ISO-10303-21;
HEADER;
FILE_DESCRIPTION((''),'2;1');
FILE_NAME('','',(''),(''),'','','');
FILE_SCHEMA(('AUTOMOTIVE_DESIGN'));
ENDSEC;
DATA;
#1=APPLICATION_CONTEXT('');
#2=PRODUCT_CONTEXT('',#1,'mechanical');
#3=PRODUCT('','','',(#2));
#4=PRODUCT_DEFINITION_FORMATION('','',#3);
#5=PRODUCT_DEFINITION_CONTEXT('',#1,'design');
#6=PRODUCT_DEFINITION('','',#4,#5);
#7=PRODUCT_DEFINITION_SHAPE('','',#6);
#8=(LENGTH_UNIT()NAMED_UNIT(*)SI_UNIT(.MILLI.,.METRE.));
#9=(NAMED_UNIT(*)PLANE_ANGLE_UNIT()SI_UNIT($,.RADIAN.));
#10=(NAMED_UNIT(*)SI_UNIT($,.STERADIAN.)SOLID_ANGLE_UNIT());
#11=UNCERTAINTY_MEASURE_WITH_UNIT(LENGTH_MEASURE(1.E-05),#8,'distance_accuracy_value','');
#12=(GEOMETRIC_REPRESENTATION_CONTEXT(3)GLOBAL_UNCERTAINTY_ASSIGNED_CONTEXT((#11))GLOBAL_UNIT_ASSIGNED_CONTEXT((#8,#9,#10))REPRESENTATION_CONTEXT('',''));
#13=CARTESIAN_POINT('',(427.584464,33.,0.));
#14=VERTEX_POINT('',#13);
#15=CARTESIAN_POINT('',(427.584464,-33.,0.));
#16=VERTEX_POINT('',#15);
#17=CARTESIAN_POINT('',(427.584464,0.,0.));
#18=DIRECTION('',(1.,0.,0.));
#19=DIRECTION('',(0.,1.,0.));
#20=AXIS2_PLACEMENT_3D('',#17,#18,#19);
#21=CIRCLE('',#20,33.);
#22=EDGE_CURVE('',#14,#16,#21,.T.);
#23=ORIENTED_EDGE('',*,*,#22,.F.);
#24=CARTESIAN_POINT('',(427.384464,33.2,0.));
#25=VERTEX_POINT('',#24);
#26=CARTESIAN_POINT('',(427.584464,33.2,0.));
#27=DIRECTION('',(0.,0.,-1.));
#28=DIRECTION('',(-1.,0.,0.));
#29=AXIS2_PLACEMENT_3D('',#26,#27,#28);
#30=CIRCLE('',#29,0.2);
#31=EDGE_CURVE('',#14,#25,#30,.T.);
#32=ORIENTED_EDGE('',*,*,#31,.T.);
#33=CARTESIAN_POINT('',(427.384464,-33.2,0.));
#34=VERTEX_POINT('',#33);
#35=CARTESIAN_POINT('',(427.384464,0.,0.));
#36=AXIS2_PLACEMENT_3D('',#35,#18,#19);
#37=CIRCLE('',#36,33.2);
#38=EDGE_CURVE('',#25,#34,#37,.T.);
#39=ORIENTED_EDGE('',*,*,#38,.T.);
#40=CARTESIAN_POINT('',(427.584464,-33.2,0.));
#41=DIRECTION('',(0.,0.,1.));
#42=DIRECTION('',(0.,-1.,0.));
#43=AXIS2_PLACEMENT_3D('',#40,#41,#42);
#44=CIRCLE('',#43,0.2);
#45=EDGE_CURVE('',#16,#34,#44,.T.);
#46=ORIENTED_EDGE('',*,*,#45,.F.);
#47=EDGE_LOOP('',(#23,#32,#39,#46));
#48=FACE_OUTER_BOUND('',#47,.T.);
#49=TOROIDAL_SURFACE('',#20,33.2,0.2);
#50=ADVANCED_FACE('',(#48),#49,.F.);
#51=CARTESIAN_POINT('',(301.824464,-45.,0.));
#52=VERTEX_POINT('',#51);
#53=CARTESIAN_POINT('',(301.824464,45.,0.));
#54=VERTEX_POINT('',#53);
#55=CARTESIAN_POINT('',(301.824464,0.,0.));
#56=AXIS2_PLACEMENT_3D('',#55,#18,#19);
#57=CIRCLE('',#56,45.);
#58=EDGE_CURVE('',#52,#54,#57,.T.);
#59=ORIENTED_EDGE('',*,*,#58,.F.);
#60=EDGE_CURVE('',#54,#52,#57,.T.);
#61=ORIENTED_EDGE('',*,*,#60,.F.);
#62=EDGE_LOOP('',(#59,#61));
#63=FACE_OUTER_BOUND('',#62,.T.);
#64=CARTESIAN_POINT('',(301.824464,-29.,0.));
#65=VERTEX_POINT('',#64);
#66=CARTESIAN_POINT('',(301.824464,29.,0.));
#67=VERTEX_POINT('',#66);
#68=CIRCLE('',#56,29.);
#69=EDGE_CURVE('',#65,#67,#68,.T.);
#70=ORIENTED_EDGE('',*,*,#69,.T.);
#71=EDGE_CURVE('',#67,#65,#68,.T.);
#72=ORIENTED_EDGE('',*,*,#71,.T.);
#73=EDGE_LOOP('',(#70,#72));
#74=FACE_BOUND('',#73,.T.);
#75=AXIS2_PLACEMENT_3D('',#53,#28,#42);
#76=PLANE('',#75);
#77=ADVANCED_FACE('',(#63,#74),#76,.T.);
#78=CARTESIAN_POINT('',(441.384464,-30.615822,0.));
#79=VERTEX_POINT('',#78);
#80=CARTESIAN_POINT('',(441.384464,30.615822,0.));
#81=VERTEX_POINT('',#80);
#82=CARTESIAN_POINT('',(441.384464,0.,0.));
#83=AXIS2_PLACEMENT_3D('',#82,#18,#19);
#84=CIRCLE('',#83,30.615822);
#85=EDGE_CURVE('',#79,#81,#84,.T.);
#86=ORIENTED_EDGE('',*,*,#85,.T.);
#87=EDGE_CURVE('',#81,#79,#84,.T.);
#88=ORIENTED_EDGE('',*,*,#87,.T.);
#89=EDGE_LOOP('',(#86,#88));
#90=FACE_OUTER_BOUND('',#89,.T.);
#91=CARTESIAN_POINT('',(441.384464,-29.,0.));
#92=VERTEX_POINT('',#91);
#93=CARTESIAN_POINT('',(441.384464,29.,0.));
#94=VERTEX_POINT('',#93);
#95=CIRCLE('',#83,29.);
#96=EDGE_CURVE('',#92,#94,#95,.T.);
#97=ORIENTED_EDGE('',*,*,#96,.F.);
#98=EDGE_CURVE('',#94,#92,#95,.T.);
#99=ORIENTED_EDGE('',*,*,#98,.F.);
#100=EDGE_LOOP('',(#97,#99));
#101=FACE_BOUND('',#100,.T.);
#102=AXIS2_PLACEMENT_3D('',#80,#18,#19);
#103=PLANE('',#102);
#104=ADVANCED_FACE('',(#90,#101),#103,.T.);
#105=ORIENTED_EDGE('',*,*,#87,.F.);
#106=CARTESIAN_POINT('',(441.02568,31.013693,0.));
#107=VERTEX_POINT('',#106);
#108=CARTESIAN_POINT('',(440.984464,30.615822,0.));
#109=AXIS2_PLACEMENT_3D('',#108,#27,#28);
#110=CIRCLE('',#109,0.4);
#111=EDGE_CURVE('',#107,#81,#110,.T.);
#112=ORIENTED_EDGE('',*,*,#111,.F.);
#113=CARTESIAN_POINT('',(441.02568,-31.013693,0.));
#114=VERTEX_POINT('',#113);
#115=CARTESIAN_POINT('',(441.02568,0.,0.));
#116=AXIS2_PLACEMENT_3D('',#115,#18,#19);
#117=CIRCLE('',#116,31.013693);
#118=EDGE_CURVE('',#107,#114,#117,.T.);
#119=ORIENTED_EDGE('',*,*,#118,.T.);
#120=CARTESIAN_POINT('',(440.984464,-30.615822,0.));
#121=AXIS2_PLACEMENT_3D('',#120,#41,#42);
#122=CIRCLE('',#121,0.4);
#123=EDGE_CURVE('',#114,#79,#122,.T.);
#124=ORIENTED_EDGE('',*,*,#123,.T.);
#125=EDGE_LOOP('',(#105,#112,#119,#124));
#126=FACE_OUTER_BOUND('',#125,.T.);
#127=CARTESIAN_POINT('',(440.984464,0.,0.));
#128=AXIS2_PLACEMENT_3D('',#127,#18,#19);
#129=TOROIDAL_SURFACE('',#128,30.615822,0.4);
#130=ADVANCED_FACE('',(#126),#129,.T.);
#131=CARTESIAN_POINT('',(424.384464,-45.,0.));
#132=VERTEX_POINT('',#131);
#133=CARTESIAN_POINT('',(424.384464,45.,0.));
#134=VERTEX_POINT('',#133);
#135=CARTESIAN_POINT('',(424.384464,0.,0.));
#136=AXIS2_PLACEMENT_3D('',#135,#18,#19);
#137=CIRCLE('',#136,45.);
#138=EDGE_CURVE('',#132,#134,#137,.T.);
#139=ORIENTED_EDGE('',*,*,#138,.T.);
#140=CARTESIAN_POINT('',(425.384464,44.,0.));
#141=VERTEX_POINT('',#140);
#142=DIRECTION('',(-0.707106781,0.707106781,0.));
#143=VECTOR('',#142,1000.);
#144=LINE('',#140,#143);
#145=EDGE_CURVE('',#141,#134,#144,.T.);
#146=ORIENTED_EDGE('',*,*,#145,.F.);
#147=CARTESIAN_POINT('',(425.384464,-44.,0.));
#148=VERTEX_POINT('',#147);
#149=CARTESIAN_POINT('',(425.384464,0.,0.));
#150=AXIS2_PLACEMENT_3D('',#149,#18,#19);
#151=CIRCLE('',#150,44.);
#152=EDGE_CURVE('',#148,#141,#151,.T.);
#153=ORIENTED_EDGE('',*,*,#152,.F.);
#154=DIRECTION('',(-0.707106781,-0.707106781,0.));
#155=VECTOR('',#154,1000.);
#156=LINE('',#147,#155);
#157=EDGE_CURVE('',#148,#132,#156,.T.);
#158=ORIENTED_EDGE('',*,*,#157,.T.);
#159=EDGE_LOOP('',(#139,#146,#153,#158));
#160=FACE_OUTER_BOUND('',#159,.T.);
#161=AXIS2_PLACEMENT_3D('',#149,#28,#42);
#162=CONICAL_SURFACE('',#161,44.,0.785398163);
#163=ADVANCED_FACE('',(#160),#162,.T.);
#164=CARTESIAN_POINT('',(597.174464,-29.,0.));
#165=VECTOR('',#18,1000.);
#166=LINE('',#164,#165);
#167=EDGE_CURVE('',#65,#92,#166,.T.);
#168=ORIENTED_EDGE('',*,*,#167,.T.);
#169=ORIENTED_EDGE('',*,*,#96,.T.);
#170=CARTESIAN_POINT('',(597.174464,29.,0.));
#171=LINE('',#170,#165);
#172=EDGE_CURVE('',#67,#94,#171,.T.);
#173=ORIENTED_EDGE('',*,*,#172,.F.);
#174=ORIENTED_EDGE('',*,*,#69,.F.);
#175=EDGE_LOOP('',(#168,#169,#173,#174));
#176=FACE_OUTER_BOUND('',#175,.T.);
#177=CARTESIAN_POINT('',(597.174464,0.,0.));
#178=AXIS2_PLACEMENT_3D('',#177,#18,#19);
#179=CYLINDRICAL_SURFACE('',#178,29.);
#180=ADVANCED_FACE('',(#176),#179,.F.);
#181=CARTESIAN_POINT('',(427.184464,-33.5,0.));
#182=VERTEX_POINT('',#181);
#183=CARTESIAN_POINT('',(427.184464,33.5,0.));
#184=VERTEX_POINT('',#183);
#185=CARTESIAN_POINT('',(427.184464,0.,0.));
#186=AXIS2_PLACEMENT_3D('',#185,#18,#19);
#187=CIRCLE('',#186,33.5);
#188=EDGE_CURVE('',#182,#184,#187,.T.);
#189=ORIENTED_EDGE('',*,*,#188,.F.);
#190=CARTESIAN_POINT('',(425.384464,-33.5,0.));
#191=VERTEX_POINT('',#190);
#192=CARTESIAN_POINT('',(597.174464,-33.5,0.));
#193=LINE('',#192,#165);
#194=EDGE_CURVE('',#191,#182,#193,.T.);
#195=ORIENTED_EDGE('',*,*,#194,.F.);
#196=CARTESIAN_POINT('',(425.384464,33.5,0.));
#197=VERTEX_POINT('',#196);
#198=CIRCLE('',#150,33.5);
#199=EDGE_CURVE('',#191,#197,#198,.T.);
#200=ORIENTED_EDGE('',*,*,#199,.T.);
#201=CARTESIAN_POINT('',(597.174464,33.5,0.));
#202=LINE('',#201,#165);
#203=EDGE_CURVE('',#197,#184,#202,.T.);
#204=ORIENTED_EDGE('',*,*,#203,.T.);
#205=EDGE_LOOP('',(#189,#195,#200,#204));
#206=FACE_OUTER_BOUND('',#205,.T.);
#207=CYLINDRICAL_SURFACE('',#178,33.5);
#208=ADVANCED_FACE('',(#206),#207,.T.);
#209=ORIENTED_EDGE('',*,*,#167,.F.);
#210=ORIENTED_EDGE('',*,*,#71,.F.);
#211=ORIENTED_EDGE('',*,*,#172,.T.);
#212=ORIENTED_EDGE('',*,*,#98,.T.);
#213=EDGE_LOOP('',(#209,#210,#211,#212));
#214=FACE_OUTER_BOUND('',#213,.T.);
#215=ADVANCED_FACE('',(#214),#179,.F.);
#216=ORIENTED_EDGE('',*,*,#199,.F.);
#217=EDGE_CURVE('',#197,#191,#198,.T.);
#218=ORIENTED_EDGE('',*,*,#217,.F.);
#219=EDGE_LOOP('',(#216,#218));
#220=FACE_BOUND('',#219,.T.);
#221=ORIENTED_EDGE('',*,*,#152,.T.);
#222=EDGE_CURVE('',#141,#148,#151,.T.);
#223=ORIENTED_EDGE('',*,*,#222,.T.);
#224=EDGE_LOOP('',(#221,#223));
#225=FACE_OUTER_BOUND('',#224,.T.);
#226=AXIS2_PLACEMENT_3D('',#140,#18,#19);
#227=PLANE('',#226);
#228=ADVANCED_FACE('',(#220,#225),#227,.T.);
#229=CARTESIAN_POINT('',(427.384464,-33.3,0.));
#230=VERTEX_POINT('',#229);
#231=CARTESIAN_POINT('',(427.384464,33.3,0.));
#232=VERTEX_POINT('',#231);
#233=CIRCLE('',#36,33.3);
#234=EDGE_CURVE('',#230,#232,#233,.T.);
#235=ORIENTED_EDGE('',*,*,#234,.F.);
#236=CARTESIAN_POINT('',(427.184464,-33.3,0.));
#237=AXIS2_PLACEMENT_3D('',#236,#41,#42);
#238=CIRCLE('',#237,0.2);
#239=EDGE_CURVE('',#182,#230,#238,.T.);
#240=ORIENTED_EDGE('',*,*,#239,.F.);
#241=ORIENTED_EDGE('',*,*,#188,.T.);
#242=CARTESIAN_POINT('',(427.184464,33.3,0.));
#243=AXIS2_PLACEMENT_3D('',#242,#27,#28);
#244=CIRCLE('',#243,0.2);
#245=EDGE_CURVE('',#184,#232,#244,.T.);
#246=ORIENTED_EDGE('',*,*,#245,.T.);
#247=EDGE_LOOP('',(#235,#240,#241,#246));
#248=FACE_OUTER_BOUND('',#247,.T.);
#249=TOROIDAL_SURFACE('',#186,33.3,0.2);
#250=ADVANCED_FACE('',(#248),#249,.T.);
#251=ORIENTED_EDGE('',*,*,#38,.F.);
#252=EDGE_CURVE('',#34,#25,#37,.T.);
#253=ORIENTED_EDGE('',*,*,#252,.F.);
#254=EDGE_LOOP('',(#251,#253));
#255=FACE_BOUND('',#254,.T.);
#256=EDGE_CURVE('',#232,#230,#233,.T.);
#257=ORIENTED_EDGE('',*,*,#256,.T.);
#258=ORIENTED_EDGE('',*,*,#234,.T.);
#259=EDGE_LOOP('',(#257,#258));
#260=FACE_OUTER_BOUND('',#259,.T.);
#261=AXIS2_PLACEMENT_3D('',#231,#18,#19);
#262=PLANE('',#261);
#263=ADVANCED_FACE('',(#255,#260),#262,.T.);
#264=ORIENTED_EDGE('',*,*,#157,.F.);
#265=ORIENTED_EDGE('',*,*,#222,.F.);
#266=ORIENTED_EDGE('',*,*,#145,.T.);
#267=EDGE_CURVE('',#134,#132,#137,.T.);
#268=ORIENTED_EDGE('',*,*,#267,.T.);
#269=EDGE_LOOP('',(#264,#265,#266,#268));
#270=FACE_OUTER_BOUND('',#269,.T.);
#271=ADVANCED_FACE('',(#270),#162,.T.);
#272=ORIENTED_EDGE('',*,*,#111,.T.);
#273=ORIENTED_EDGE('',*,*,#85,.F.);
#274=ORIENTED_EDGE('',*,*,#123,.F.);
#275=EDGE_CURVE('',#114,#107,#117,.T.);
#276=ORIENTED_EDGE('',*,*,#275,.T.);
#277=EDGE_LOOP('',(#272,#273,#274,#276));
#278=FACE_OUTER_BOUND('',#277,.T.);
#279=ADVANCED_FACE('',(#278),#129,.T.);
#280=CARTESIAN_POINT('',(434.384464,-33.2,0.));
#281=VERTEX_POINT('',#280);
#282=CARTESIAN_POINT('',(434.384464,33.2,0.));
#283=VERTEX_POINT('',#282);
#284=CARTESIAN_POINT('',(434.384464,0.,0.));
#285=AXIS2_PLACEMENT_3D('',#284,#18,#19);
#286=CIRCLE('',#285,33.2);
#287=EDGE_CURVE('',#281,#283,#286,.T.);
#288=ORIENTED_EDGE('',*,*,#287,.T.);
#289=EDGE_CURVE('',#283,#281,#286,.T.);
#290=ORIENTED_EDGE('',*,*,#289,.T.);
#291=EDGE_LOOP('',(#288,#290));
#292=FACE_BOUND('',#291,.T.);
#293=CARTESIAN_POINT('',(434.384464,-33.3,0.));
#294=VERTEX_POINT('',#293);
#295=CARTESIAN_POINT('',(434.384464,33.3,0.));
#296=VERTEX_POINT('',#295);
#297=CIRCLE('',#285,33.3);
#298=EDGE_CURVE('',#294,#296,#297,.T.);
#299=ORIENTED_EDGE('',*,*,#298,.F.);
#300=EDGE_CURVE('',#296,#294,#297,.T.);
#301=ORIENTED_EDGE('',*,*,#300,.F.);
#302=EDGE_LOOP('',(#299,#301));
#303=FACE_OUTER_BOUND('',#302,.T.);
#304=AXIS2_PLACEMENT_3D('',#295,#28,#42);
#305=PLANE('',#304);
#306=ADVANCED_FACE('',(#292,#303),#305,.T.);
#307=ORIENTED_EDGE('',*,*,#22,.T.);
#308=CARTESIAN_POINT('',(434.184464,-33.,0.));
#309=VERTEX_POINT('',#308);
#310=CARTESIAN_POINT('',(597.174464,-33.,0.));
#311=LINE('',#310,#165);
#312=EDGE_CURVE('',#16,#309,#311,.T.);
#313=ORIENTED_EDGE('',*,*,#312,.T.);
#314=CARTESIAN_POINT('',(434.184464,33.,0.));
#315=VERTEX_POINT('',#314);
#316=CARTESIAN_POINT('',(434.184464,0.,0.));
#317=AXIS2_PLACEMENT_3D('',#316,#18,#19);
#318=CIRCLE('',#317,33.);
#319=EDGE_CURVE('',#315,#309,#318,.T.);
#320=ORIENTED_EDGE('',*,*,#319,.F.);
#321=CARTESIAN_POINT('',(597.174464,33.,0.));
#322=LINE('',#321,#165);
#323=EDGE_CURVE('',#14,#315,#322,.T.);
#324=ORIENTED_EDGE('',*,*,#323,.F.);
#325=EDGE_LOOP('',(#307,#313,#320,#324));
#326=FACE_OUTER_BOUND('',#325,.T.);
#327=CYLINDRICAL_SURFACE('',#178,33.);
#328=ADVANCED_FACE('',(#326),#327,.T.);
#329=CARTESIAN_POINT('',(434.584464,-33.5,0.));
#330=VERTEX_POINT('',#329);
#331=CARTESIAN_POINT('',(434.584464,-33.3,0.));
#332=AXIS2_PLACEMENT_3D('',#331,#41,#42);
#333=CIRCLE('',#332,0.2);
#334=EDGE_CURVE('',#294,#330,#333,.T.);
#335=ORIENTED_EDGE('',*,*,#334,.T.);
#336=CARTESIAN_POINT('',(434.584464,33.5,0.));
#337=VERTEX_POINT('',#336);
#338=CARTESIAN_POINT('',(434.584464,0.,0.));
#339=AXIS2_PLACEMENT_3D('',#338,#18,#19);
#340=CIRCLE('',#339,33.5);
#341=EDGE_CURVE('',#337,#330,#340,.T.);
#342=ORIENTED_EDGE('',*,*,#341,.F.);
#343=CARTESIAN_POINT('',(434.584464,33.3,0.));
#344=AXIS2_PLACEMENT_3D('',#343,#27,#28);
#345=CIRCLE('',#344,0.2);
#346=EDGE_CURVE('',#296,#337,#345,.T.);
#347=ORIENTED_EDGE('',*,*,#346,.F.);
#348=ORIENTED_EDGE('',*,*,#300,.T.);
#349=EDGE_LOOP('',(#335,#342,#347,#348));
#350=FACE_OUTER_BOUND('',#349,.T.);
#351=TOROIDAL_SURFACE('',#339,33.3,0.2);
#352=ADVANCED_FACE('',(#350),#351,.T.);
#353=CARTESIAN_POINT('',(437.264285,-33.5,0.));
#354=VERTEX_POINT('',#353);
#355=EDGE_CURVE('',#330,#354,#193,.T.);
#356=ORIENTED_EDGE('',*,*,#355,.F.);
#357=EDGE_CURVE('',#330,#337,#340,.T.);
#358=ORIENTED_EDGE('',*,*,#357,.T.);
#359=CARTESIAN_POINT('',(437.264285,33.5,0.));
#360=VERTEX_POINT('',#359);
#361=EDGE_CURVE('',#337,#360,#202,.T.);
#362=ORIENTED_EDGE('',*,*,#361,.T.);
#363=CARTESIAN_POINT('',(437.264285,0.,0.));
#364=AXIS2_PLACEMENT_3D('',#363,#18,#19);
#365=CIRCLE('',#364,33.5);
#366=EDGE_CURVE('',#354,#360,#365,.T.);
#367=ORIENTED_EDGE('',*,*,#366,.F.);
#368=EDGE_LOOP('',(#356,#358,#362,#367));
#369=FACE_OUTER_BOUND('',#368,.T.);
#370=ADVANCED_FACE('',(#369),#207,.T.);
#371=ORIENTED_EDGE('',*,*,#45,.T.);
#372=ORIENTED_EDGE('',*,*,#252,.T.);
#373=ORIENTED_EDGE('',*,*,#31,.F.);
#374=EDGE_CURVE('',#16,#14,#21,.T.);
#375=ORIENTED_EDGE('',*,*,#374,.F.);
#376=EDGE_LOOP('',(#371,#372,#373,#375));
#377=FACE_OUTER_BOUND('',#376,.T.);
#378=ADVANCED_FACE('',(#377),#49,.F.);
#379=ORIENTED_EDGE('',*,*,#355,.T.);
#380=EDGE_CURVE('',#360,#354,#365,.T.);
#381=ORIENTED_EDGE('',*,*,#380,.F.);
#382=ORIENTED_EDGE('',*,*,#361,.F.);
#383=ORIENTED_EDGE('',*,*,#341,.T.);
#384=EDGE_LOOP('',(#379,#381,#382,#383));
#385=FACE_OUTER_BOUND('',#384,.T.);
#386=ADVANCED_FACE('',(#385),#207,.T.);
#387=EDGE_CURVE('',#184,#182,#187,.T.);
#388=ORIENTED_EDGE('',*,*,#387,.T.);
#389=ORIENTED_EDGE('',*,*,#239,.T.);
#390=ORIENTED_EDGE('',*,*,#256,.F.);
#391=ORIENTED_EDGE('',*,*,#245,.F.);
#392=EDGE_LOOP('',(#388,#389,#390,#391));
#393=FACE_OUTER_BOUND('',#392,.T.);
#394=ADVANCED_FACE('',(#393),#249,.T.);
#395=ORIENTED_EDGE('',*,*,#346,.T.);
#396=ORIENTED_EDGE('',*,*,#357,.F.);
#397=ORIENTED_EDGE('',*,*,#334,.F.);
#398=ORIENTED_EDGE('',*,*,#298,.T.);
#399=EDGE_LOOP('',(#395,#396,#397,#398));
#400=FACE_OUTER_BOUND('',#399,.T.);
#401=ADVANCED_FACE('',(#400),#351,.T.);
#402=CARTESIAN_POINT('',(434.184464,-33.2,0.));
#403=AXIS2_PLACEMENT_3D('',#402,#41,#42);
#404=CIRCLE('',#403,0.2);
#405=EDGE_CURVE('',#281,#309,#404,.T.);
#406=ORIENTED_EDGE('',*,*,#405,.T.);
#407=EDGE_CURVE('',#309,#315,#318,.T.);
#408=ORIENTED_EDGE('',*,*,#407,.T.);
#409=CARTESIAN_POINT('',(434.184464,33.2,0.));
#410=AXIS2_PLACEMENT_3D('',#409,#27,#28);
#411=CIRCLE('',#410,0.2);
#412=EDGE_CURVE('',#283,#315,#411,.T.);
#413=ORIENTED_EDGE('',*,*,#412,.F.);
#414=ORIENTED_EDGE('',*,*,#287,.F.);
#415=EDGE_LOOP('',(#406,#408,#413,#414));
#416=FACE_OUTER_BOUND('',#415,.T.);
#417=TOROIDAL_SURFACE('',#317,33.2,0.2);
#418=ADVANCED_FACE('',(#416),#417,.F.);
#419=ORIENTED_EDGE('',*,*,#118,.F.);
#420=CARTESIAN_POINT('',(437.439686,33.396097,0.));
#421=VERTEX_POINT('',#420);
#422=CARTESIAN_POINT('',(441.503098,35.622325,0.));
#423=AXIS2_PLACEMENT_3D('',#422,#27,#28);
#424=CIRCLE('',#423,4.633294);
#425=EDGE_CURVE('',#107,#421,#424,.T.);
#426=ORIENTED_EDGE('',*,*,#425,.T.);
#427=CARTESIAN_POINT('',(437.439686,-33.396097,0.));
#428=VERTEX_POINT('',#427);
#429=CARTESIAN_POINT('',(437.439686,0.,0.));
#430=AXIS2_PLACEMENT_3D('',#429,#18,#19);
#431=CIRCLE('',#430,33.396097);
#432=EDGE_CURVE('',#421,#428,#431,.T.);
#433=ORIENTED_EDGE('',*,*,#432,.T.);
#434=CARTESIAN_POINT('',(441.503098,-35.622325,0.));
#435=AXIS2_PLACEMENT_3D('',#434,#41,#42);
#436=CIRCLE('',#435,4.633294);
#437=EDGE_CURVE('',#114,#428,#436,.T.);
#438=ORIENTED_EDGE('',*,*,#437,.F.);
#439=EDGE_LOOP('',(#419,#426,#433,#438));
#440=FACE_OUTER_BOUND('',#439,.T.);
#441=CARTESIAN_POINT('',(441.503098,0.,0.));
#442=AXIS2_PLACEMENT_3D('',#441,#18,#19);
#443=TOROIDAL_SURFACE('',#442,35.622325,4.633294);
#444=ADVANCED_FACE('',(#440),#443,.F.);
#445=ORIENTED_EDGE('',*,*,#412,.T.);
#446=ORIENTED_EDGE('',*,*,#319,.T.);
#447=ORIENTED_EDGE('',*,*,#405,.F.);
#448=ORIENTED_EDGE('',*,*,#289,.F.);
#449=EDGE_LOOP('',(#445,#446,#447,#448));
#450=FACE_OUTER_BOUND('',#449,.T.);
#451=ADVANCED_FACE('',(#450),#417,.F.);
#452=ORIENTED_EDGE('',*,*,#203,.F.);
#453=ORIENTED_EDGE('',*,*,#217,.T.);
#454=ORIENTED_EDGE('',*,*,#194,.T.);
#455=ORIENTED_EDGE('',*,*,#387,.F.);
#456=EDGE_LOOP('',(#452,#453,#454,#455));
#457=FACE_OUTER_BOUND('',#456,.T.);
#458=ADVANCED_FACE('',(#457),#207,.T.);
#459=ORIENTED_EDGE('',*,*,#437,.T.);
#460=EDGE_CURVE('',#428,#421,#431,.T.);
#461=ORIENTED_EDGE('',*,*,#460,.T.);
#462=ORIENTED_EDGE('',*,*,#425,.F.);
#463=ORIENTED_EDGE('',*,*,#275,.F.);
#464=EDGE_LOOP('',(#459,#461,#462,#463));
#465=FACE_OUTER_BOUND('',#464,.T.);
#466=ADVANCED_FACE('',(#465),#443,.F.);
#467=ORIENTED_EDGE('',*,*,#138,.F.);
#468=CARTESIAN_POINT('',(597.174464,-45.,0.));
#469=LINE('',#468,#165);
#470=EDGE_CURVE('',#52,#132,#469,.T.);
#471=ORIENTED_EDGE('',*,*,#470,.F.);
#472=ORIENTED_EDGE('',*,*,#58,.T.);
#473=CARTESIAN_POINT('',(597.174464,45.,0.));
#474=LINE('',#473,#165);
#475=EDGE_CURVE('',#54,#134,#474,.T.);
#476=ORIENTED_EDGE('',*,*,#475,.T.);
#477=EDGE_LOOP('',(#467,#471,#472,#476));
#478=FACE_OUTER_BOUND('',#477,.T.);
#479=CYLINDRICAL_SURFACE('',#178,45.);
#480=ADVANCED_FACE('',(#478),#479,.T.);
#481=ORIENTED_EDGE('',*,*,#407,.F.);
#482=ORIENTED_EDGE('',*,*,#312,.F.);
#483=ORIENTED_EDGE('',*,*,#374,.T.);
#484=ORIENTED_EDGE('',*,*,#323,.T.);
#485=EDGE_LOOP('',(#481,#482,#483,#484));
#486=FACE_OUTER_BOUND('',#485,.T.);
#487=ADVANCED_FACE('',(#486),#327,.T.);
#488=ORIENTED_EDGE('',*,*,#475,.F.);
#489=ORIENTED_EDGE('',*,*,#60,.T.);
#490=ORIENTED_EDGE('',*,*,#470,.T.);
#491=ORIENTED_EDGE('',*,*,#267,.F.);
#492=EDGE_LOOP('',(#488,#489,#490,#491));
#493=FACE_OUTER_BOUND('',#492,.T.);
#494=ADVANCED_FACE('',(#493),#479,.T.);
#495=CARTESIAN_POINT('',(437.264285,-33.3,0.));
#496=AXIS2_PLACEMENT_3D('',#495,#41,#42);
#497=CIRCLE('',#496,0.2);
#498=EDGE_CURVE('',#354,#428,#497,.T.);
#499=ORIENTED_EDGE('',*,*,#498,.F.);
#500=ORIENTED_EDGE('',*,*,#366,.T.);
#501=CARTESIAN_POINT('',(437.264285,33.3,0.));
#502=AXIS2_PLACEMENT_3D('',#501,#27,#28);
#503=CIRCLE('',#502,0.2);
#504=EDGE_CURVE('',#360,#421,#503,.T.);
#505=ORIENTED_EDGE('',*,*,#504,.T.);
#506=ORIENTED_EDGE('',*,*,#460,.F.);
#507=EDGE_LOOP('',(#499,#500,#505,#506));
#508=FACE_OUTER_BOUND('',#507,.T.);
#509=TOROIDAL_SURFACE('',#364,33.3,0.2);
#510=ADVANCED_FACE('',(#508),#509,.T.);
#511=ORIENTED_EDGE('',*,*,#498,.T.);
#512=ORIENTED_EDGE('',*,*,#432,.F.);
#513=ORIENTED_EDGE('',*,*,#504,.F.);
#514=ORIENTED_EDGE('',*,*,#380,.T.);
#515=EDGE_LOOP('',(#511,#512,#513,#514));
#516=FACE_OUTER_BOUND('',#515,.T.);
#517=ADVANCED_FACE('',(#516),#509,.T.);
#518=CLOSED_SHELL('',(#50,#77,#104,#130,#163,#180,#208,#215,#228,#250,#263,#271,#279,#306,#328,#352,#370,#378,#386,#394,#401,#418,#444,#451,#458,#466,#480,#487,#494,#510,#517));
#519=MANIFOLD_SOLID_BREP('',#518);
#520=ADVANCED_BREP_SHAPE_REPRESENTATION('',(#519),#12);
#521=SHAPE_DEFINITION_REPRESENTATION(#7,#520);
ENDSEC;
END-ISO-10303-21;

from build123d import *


with BuildPart() as part:
    # Sketch1 → Revolve1 (revolve)
    with BuildSketch(Plane.XY):
        with BuildLine():
            Line((437.264284999, 33.5), (434.584463757, 33.5))
            ThreePointArc((434.584463757, 33.5), (434.443042401, 33.441421356), (434.384463757, 33.3))
            Line((434.384463757, 33.3), (434.384463757, 33.2))
            ThreePointArc((434.384463757, 33.2), (434.325885113, 33.058578644), (434.184463757, 33))
            Line((434.184463757, 33), (427.584463757, 33))
            ThreePointArc((427.584463757, 33), (427.443042401, 33.058578644), (427.384463757, 33.2))
            Line((427.384463757, 33.2), (427.384463757, 33.3))
            ThreePointArc((427.384463757, 33.3), (427.325885113, 33.441421356), (427.184463757, 33.5))
            Line((427.184463757, 33.5), (425.384463757, 33.5))
            Line((425.384463757, 33.5), (425.384463757, 44))
            Line((425.384463757, 44), (424.384463757, 45))
            Line((424.384463757, 45), (411.824463757, 45))
            Line((411.824463757, 45), (391.824463757, 45))
            Line((391.824463757, 45), (301.824463757, 45))
            Line((301.824463757, 45), (301.824463757, 29))
            Line((301.824463757, 29), (441.384463757, 29))
            Line((441.384463757, 29), (441.384463757, 30.615822229))
            ThreePointArc((441.384463757, 30.615822229), (441.281521436, 30.883696706), (441.02568008, 31.013693081))
            ThreePointArc((441.02568008, 31.013693081), (438.939166095, 31.763093605), (437.439685601, 33.396096976))
            ThreePointArc((437.439685601, 33.396096976), (437.366217832, 33.472074686), (437.264284999, 33.5))
        make_face()
    revolve(axis=Axis((597.174463757, 0, 0), (-1, 0, 0)))


solid = part.part
